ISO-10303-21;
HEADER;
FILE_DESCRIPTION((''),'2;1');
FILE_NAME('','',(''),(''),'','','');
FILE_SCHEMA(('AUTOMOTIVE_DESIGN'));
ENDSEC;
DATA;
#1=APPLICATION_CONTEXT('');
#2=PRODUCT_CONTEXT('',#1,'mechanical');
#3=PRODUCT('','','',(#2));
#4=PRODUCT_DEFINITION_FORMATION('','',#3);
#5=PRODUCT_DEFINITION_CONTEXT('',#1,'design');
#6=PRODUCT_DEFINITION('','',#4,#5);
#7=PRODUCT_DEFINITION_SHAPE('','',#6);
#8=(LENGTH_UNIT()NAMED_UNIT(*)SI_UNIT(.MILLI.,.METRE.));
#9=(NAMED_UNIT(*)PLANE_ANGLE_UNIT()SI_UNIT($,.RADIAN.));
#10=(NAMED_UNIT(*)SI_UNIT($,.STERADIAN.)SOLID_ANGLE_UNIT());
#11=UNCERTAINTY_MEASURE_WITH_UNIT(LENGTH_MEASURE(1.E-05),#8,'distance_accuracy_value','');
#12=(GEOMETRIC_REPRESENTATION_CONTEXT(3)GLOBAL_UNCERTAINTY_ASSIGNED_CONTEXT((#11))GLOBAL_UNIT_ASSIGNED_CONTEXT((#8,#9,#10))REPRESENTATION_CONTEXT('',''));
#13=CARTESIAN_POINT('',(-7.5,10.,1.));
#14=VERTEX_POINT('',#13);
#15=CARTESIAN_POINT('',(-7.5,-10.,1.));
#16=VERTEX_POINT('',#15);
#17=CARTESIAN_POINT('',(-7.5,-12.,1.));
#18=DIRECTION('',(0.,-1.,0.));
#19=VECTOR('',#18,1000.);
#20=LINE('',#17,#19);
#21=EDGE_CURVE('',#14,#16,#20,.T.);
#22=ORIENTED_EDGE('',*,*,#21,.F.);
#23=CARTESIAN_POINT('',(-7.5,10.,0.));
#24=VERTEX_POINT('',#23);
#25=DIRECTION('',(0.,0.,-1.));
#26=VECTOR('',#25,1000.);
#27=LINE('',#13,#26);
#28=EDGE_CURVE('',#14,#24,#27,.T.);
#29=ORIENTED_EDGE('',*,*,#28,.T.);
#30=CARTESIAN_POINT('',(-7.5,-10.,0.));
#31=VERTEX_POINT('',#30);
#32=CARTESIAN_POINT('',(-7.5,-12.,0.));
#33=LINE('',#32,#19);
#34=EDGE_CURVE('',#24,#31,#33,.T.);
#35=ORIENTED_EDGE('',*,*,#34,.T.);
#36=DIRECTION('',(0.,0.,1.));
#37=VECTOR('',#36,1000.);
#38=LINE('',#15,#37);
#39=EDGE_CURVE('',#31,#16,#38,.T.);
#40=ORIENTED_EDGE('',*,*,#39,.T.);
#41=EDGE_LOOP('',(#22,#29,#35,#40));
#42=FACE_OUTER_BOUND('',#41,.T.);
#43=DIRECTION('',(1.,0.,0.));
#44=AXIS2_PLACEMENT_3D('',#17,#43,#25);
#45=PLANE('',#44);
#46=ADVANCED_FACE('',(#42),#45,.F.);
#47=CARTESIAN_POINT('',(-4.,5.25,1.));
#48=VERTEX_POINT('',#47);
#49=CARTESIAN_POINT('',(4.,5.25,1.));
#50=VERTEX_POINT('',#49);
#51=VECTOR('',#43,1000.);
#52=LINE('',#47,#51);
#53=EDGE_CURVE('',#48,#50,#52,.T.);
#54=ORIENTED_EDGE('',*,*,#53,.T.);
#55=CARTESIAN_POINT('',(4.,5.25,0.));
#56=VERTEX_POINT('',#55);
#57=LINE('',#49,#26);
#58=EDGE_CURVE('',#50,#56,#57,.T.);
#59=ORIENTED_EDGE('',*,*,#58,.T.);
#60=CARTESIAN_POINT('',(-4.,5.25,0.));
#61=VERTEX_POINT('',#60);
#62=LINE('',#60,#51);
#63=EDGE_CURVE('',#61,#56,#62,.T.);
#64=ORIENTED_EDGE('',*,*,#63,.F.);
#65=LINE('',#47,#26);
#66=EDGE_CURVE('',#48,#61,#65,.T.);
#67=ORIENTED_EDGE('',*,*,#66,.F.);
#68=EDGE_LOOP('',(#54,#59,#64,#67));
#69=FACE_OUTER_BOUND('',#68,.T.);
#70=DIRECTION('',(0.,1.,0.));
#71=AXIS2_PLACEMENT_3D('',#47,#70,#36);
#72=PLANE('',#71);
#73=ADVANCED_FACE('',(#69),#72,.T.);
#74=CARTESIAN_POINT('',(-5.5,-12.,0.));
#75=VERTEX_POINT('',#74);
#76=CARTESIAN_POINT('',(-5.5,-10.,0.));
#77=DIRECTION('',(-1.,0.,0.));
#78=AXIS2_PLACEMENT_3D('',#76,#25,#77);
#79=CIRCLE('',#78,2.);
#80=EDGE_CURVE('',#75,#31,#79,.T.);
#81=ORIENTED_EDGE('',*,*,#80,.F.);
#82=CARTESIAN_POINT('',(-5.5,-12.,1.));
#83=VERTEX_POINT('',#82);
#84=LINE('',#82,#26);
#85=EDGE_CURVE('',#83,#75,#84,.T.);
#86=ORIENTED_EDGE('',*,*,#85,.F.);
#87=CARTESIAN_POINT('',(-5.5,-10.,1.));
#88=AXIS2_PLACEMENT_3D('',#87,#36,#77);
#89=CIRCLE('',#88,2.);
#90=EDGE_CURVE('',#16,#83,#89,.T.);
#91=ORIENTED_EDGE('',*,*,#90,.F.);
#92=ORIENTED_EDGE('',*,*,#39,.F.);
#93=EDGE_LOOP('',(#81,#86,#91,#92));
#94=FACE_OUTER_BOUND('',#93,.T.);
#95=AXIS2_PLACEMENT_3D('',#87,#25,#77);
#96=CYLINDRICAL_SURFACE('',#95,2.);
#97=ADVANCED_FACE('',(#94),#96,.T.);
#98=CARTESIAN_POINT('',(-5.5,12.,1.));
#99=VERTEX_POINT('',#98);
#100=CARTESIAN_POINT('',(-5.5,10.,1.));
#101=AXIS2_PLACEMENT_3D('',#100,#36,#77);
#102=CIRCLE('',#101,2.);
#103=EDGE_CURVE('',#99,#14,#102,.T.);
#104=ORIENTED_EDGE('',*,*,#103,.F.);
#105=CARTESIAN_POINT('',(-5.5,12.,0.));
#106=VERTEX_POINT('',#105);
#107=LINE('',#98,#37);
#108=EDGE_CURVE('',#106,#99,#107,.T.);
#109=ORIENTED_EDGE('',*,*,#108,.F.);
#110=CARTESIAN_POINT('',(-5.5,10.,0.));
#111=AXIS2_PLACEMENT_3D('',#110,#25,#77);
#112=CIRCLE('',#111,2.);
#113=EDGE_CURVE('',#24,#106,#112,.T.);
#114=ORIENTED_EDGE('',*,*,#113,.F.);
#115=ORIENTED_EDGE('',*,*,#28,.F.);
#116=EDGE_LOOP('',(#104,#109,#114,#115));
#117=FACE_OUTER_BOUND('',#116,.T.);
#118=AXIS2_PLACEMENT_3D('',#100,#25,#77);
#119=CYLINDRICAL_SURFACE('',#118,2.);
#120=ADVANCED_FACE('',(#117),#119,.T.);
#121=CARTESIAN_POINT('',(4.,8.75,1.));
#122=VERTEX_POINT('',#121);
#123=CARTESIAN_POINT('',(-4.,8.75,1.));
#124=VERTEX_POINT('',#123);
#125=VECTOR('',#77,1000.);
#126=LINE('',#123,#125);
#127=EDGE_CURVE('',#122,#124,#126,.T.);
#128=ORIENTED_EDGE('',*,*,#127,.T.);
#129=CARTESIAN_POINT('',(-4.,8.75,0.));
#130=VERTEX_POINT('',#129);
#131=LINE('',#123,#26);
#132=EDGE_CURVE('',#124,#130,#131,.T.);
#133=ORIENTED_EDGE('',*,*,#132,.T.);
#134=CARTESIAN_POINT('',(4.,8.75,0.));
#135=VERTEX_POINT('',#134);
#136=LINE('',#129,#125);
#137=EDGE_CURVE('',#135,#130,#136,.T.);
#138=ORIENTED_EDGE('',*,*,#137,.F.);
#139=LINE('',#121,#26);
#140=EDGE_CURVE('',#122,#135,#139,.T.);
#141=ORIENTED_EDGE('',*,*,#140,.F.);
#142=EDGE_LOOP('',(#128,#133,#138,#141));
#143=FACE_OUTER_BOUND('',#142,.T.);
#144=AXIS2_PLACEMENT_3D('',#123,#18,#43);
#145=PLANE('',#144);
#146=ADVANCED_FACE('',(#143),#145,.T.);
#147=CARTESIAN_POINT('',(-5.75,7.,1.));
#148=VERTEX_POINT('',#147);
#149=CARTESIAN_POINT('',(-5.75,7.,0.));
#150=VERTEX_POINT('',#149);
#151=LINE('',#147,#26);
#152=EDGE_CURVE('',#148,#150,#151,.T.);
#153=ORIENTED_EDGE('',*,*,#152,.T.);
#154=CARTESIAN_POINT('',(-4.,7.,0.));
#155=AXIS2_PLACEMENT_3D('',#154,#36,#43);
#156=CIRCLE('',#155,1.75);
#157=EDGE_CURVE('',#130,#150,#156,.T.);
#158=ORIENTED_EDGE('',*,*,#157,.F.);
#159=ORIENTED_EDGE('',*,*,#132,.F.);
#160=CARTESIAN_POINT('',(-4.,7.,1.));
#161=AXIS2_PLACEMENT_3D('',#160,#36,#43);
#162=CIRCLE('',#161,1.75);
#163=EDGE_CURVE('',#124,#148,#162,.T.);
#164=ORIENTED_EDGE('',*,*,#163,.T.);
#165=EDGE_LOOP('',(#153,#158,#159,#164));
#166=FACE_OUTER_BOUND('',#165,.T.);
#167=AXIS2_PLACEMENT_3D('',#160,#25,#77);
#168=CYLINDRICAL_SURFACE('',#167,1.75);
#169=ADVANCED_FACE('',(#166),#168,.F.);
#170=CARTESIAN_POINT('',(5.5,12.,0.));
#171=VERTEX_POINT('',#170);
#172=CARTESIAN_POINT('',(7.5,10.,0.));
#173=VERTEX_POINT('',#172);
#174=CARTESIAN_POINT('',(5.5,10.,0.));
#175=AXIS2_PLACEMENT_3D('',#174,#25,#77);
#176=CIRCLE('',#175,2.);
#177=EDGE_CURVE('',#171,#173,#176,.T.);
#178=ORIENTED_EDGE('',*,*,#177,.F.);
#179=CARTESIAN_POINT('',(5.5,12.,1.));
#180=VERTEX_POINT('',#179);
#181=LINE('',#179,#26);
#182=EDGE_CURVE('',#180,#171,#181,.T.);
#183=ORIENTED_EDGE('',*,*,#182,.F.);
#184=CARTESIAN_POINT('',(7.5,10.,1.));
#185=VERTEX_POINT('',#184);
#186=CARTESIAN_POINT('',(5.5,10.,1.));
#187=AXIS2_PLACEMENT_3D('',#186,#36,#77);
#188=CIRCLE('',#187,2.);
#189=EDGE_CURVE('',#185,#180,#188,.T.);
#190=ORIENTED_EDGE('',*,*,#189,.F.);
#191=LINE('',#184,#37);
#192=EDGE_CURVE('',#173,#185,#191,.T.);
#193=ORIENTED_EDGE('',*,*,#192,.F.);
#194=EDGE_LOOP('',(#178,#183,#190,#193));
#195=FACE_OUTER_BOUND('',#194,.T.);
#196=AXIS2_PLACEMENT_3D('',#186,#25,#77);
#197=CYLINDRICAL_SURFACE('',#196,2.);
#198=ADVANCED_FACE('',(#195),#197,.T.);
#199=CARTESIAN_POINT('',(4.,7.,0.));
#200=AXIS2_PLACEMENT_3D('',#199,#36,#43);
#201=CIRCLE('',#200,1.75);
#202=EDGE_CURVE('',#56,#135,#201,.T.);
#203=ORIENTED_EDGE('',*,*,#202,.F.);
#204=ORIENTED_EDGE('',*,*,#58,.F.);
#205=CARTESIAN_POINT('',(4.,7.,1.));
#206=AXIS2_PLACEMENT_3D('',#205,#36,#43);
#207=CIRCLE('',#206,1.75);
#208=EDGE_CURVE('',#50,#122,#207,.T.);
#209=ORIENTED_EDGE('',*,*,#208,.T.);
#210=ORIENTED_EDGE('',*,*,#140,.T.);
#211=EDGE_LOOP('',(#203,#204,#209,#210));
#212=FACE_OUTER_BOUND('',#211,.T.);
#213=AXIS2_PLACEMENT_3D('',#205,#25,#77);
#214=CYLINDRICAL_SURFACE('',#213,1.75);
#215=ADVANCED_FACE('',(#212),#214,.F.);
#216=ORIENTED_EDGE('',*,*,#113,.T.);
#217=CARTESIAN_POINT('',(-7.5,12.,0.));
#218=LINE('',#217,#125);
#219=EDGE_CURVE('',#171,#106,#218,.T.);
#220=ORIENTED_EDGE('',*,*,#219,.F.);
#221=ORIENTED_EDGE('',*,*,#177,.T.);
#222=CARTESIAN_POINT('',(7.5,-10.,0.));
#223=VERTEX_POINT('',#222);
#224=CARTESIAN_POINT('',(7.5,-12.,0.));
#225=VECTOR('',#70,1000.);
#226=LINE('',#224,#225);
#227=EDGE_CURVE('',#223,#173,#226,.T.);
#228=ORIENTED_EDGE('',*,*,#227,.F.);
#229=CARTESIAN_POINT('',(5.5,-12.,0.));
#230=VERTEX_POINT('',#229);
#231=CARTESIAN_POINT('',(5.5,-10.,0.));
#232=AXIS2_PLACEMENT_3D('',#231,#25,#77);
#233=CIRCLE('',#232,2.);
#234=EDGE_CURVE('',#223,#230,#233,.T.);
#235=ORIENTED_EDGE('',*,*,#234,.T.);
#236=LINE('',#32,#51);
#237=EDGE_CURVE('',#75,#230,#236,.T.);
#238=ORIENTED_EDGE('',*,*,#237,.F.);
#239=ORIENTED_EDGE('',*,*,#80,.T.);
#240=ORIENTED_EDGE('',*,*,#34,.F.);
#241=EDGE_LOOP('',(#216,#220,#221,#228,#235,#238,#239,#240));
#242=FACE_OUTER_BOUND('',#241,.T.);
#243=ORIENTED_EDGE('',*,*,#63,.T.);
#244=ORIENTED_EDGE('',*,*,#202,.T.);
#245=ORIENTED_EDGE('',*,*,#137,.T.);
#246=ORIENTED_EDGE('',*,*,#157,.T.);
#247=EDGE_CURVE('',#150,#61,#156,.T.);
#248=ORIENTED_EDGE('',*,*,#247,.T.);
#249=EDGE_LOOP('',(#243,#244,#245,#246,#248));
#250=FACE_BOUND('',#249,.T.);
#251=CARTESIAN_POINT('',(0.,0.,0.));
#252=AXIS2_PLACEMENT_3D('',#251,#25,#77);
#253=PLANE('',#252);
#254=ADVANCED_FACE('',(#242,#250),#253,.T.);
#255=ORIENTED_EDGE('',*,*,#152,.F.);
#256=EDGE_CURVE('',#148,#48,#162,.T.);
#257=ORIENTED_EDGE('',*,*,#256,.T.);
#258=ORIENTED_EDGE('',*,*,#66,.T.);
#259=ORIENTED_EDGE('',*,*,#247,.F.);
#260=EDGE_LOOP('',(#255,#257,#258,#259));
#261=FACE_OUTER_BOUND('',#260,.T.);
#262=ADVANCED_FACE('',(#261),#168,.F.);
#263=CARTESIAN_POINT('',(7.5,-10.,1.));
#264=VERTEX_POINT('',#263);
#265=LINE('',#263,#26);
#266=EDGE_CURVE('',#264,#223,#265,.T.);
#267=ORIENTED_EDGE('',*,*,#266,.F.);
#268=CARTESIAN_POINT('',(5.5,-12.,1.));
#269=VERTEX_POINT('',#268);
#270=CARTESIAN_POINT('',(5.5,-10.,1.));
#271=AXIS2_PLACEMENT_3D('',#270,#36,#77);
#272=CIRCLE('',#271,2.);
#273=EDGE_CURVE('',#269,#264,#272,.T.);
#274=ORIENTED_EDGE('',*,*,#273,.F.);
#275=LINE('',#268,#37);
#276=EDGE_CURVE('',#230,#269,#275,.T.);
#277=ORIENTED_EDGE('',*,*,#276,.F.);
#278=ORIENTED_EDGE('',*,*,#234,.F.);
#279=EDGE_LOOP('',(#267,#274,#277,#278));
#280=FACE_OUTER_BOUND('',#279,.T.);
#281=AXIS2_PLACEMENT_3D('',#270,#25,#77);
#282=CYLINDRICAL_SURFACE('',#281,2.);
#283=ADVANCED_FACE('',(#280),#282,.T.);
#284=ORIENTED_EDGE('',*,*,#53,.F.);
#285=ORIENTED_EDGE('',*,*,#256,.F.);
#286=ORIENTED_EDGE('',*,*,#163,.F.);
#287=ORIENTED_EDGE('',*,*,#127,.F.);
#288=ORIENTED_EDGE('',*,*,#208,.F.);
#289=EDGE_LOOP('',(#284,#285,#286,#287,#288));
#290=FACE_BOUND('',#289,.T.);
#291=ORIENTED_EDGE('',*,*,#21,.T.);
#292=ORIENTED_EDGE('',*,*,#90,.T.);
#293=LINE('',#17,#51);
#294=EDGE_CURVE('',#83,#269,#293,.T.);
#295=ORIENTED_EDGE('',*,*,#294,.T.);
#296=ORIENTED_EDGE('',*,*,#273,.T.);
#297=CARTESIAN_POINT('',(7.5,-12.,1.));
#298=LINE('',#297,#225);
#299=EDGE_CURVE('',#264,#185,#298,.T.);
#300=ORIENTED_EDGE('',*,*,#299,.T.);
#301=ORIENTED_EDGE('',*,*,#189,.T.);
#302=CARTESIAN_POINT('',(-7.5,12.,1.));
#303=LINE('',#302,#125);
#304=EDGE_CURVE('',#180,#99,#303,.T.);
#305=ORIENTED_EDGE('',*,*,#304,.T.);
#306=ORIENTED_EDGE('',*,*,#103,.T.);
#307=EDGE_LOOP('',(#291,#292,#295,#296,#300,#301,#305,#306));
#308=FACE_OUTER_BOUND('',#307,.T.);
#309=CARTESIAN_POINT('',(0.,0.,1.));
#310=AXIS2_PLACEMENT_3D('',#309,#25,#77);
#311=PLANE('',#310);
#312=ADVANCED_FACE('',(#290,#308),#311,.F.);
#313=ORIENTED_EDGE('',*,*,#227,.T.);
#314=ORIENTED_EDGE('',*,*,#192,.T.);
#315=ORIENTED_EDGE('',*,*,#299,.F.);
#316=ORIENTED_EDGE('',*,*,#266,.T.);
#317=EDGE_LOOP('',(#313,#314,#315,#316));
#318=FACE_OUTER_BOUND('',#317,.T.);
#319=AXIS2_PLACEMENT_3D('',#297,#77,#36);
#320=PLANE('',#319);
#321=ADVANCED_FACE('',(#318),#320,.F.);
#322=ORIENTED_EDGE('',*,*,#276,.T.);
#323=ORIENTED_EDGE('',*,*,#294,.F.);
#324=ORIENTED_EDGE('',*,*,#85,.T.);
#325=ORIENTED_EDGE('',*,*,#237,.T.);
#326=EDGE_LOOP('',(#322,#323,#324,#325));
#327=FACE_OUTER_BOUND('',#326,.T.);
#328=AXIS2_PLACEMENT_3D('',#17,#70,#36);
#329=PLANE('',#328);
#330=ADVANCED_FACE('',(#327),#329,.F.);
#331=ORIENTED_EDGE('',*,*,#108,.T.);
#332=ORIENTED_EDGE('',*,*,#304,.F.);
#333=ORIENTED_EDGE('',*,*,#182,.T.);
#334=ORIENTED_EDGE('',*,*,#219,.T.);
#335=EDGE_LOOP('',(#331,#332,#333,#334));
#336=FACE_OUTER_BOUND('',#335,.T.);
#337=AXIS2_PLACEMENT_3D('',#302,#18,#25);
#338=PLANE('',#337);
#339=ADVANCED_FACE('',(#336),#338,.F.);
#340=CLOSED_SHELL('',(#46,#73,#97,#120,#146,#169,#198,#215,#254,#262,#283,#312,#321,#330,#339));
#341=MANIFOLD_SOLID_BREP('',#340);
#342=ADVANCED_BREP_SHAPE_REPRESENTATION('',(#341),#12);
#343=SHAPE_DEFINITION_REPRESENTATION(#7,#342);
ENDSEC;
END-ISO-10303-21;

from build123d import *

# Parameters (mm, degrees)
SKETCH1_W           = 15
SKETCH1_H           = 24
BOSS_EXTRUDE1_DEPTH = 1
FILLET1_R           = 2


with BuildPart() as part:
    # Sketch1 → Boss-Extrude1 (new body)
    with BuildSketch(Plane.XY):
        Rectangle(SKETCH1_W, SKETCH1_H)
        with BuildLine():
            Line((-4, 8.75), (4, 8.75))
            ThreePointArc((4, 8.75), (5.75, 7), (4, 5.25))
            Line((4, 5.25), (-4, 5.25))
            ThreePointArc((-4, 5.25), (-5.75, 7), (-4, 8.75))
        make_face(mode=Mode.SUBTRACT)
    extrude(amount=BOSS_EXTRUDE1_DEPTH)

    # Fillet1
    fillet1_edges = [part.edges().sort_by_distance(p)[0] for p in [
        (7.5, -12, 0.5),
        (-7.5, -12, 0.5),
        (-7.5, 12, 0.5),
        (7.5, 12, 0.5),
    ]]
    fillet(fillet1_edges, radius=FILLET1_R)


solid = part.part
